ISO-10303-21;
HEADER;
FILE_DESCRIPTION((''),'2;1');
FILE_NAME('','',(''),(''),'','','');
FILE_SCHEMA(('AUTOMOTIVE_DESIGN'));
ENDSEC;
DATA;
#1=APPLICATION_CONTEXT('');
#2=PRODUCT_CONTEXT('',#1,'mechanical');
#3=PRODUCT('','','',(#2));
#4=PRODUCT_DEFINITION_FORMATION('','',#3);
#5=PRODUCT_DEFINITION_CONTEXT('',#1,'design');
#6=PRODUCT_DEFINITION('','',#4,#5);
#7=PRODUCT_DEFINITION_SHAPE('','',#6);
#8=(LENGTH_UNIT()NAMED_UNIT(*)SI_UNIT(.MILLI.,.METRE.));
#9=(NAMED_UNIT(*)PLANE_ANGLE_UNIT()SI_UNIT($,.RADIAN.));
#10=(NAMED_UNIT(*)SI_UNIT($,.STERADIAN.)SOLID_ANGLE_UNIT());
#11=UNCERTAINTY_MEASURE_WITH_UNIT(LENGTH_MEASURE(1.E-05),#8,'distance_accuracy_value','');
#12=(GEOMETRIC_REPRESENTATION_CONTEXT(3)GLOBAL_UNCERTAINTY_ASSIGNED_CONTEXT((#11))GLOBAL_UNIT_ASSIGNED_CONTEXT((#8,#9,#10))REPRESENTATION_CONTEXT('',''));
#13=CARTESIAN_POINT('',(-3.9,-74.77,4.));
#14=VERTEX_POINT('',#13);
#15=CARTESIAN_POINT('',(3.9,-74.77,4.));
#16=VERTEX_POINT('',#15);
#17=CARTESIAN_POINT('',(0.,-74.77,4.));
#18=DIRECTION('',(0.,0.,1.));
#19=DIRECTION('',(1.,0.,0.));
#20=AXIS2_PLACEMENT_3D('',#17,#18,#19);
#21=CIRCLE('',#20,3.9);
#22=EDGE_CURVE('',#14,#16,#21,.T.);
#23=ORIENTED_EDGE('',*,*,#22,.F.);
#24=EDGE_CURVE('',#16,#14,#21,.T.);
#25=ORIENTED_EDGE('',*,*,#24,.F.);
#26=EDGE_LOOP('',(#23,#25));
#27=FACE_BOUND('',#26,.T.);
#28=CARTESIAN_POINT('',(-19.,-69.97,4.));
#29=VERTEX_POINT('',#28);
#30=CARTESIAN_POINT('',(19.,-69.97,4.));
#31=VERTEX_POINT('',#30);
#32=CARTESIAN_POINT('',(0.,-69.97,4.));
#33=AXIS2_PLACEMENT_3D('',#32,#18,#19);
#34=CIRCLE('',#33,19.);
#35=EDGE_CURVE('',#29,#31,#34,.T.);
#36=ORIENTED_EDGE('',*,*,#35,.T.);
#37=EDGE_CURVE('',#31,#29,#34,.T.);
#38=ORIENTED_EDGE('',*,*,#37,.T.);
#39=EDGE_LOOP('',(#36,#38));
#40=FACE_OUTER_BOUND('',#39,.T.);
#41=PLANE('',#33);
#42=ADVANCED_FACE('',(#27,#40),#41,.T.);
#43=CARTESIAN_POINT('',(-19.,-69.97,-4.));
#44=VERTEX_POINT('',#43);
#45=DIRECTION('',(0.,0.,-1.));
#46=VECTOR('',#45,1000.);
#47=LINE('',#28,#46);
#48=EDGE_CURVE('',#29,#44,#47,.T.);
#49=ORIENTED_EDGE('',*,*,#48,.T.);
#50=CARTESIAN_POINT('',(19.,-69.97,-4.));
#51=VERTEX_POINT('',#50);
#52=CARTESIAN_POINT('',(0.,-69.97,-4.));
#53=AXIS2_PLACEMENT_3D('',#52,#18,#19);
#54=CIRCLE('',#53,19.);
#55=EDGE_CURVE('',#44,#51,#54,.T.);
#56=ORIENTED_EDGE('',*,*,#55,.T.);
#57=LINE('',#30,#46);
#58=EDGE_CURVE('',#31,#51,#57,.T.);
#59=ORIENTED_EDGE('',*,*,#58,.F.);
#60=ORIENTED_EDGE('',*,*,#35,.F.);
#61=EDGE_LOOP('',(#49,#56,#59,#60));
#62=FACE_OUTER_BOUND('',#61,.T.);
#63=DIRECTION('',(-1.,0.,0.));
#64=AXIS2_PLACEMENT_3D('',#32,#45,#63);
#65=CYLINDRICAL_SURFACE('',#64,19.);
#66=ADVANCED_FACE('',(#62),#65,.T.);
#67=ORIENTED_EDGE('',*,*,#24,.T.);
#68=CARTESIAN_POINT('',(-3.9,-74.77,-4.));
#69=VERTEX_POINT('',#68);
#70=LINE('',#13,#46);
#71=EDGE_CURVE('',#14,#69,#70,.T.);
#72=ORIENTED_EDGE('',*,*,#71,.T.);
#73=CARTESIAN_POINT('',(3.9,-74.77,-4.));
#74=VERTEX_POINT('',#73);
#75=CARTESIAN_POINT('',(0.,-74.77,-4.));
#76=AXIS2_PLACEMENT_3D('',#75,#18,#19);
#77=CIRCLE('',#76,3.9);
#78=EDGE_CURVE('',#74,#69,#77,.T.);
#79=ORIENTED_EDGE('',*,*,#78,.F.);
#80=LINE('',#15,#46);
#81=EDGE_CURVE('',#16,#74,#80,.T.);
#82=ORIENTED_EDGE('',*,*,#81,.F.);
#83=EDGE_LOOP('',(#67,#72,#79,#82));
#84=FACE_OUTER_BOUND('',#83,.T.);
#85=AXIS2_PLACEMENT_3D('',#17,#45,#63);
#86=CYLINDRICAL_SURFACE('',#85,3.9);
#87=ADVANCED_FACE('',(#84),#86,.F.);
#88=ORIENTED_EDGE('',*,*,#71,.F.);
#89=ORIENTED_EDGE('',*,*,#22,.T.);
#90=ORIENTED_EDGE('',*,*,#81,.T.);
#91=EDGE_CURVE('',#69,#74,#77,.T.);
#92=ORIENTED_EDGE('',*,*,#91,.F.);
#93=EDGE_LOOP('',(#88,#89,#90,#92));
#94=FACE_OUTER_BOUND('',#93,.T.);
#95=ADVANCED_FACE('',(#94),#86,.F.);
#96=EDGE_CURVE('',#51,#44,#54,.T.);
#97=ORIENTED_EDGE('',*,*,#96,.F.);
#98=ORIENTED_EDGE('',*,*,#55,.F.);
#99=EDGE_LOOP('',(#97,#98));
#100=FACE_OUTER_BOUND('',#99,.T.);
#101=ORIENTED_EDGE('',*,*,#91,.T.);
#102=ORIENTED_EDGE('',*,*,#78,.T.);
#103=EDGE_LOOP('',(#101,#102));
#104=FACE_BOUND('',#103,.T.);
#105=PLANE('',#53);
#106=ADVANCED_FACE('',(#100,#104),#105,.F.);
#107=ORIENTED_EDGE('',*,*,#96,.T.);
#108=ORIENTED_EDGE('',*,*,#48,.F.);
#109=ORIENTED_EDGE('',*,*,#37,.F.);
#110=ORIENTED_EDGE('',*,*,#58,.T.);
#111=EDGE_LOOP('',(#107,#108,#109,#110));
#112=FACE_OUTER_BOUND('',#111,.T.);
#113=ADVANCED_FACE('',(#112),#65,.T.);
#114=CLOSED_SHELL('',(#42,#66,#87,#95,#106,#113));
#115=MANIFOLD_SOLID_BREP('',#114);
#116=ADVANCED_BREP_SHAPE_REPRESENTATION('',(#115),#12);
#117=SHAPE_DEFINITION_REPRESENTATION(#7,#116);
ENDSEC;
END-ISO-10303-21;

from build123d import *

# Parameters (mm, degrees)
SKETCH1_R           = 19
SKETCH1_R_2         = 3.9
BOSS_EXTRUDE1_DEPTH = 4


with BuildPart() as part:
    # Sketch1 → Boss-Extrude1 (new, symmetric)
    with BuildSketch(Plane.XY):
        with Locations((0, -69.97)):
            Circle(SKETCH1_R)
        with Locations((0, -74.77)):
            Circle(SKETCH1_R_2, mode=Mode.SUBTRACT)
    extrude(amount=BOSS_EXTRUDE1_DEPTH, both=True)


solid = part.part
